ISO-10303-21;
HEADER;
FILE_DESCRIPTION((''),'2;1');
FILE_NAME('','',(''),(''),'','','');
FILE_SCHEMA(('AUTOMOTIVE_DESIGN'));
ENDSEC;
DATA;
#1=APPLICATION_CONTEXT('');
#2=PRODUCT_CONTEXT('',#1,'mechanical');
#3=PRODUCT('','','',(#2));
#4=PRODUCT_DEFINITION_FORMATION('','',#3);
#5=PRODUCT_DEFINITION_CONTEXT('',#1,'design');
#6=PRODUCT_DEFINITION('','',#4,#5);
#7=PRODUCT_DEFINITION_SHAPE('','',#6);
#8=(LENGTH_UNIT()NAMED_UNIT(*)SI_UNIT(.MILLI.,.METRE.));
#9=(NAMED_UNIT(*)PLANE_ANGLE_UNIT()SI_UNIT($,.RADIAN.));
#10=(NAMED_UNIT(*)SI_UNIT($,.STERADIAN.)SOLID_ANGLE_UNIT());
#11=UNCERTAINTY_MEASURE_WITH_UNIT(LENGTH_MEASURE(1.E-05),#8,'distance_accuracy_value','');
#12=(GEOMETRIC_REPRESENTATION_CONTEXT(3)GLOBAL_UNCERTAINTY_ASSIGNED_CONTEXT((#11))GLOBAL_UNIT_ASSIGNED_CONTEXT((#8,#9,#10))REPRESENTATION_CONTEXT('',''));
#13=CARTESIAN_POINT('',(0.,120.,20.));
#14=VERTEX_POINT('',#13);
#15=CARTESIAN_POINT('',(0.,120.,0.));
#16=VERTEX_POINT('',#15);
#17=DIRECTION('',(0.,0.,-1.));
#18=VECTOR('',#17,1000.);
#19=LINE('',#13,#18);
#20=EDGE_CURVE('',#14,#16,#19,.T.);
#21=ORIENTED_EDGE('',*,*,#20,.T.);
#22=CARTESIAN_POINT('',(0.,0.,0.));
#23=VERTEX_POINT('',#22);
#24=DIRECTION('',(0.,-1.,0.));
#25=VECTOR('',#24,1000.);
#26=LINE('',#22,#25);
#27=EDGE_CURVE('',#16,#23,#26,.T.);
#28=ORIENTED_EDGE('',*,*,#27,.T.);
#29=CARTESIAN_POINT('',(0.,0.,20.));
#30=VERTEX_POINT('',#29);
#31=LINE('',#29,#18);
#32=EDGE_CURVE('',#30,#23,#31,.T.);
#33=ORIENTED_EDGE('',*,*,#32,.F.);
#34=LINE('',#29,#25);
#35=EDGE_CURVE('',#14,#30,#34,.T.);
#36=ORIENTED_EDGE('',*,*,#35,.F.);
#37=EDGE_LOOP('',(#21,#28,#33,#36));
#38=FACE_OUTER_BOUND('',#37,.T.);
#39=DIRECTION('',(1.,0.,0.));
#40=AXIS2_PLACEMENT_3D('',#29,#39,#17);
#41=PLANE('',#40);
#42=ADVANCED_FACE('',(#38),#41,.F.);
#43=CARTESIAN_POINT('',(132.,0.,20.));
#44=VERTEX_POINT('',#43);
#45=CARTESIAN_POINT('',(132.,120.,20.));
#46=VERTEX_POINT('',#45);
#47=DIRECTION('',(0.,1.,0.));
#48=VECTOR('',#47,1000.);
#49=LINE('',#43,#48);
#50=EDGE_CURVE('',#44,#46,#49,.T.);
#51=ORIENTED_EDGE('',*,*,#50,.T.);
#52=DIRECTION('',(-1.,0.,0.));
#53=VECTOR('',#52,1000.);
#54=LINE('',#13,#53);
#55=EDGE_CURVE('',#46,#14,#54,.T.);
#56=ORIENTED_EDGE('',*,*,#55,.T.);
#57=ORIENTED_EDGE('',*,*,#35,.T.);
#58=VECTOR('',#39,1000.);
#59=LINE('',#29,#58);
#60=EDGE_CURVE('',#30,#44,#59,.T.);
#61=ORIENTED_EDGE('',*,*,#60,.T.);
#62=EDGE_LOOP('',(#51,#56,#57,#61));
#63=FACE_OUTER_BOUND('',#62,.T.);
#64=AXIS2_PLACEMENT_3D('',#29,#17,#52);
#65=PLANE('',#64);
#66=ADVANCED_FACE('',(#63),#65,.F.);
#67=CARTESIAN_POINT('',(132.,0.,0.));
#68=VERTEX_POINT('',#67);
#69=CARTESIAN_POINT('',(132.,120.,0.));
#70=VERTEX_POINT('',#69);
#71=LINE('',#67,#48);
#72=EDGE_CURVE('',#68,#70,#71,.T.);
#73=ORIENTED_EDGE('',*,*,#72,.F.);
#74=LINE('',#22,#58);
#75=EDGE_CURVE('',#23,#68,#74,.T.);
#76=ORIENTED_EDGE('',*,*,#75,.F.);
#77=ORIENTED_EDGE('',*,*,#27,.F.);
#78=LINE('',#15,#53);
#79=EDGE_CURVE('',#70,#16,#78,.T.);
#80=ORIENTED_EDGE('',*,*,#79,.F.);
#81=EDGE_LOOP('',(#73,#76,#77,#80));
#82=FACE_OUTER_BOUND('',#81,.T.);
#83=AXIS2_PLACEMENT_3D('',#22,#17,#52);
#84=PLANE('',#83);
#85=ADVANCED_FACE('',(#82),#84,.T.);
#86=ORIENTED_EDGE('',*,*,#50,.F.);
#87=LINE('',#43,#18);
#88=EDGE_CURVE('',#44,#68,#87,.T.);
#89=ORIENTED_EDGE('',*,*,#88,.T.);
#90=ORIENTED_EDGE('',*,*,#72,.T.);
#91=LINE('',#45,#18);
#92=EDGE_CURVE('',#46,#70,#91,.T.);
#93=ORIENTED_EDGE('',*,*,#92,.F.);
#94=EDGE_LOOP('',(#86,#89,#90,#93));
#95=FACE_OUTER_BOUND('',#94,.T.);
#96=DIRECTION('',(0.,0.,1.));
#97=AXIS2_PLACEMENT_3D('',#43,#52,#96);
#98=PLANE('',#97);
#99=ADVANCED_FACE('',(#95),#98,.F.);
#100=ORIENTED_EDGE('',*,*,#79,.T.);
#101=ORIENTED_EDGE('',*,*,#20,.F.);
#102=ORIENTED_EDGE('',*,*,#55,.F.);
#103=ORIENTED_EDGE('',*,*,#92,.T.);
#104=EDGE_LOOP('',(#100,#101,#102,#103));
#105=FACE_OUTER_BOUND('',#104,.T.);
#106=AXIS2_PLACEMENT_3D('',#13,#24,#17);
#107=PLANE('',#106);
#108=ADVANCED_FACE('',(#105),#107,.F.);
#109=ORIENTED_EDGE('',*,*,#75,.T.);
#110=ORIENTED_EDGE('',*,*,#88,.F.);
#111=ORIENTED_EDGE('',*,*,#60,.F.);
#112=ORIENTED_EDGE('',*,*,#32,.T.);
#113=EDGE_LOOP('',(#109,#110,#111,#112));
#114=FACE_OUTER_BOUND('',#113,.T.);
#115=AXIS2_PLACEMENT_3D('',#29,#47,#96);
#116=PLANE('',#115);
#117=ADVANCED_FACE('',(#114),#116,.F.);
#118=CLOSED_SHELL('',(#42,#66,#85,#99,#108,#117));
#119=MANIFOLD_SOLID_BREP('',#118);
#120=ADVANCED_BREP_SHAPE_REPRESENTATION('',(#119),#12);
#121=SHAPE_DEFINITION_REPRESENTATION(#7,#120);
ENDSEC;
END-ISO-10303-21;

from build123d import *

# Parameters (mm, degrees)
SKETCH1_W           = 132
SKETCH1_H           = 120
BOSS_EXTRUDE1_DEPTH = 20


with BuildPart() as part:
    # Sketch1 → Boss-Extrude1 (new body)
    with BuildSketch(Plane.XY):
        with Locations((66, 60)):
            Rectangle(SKETCH1_W, SKETCH1_H)
    extrude(amount=BOSS_EXTRUDE1_DEPTH)


solid = part.part
